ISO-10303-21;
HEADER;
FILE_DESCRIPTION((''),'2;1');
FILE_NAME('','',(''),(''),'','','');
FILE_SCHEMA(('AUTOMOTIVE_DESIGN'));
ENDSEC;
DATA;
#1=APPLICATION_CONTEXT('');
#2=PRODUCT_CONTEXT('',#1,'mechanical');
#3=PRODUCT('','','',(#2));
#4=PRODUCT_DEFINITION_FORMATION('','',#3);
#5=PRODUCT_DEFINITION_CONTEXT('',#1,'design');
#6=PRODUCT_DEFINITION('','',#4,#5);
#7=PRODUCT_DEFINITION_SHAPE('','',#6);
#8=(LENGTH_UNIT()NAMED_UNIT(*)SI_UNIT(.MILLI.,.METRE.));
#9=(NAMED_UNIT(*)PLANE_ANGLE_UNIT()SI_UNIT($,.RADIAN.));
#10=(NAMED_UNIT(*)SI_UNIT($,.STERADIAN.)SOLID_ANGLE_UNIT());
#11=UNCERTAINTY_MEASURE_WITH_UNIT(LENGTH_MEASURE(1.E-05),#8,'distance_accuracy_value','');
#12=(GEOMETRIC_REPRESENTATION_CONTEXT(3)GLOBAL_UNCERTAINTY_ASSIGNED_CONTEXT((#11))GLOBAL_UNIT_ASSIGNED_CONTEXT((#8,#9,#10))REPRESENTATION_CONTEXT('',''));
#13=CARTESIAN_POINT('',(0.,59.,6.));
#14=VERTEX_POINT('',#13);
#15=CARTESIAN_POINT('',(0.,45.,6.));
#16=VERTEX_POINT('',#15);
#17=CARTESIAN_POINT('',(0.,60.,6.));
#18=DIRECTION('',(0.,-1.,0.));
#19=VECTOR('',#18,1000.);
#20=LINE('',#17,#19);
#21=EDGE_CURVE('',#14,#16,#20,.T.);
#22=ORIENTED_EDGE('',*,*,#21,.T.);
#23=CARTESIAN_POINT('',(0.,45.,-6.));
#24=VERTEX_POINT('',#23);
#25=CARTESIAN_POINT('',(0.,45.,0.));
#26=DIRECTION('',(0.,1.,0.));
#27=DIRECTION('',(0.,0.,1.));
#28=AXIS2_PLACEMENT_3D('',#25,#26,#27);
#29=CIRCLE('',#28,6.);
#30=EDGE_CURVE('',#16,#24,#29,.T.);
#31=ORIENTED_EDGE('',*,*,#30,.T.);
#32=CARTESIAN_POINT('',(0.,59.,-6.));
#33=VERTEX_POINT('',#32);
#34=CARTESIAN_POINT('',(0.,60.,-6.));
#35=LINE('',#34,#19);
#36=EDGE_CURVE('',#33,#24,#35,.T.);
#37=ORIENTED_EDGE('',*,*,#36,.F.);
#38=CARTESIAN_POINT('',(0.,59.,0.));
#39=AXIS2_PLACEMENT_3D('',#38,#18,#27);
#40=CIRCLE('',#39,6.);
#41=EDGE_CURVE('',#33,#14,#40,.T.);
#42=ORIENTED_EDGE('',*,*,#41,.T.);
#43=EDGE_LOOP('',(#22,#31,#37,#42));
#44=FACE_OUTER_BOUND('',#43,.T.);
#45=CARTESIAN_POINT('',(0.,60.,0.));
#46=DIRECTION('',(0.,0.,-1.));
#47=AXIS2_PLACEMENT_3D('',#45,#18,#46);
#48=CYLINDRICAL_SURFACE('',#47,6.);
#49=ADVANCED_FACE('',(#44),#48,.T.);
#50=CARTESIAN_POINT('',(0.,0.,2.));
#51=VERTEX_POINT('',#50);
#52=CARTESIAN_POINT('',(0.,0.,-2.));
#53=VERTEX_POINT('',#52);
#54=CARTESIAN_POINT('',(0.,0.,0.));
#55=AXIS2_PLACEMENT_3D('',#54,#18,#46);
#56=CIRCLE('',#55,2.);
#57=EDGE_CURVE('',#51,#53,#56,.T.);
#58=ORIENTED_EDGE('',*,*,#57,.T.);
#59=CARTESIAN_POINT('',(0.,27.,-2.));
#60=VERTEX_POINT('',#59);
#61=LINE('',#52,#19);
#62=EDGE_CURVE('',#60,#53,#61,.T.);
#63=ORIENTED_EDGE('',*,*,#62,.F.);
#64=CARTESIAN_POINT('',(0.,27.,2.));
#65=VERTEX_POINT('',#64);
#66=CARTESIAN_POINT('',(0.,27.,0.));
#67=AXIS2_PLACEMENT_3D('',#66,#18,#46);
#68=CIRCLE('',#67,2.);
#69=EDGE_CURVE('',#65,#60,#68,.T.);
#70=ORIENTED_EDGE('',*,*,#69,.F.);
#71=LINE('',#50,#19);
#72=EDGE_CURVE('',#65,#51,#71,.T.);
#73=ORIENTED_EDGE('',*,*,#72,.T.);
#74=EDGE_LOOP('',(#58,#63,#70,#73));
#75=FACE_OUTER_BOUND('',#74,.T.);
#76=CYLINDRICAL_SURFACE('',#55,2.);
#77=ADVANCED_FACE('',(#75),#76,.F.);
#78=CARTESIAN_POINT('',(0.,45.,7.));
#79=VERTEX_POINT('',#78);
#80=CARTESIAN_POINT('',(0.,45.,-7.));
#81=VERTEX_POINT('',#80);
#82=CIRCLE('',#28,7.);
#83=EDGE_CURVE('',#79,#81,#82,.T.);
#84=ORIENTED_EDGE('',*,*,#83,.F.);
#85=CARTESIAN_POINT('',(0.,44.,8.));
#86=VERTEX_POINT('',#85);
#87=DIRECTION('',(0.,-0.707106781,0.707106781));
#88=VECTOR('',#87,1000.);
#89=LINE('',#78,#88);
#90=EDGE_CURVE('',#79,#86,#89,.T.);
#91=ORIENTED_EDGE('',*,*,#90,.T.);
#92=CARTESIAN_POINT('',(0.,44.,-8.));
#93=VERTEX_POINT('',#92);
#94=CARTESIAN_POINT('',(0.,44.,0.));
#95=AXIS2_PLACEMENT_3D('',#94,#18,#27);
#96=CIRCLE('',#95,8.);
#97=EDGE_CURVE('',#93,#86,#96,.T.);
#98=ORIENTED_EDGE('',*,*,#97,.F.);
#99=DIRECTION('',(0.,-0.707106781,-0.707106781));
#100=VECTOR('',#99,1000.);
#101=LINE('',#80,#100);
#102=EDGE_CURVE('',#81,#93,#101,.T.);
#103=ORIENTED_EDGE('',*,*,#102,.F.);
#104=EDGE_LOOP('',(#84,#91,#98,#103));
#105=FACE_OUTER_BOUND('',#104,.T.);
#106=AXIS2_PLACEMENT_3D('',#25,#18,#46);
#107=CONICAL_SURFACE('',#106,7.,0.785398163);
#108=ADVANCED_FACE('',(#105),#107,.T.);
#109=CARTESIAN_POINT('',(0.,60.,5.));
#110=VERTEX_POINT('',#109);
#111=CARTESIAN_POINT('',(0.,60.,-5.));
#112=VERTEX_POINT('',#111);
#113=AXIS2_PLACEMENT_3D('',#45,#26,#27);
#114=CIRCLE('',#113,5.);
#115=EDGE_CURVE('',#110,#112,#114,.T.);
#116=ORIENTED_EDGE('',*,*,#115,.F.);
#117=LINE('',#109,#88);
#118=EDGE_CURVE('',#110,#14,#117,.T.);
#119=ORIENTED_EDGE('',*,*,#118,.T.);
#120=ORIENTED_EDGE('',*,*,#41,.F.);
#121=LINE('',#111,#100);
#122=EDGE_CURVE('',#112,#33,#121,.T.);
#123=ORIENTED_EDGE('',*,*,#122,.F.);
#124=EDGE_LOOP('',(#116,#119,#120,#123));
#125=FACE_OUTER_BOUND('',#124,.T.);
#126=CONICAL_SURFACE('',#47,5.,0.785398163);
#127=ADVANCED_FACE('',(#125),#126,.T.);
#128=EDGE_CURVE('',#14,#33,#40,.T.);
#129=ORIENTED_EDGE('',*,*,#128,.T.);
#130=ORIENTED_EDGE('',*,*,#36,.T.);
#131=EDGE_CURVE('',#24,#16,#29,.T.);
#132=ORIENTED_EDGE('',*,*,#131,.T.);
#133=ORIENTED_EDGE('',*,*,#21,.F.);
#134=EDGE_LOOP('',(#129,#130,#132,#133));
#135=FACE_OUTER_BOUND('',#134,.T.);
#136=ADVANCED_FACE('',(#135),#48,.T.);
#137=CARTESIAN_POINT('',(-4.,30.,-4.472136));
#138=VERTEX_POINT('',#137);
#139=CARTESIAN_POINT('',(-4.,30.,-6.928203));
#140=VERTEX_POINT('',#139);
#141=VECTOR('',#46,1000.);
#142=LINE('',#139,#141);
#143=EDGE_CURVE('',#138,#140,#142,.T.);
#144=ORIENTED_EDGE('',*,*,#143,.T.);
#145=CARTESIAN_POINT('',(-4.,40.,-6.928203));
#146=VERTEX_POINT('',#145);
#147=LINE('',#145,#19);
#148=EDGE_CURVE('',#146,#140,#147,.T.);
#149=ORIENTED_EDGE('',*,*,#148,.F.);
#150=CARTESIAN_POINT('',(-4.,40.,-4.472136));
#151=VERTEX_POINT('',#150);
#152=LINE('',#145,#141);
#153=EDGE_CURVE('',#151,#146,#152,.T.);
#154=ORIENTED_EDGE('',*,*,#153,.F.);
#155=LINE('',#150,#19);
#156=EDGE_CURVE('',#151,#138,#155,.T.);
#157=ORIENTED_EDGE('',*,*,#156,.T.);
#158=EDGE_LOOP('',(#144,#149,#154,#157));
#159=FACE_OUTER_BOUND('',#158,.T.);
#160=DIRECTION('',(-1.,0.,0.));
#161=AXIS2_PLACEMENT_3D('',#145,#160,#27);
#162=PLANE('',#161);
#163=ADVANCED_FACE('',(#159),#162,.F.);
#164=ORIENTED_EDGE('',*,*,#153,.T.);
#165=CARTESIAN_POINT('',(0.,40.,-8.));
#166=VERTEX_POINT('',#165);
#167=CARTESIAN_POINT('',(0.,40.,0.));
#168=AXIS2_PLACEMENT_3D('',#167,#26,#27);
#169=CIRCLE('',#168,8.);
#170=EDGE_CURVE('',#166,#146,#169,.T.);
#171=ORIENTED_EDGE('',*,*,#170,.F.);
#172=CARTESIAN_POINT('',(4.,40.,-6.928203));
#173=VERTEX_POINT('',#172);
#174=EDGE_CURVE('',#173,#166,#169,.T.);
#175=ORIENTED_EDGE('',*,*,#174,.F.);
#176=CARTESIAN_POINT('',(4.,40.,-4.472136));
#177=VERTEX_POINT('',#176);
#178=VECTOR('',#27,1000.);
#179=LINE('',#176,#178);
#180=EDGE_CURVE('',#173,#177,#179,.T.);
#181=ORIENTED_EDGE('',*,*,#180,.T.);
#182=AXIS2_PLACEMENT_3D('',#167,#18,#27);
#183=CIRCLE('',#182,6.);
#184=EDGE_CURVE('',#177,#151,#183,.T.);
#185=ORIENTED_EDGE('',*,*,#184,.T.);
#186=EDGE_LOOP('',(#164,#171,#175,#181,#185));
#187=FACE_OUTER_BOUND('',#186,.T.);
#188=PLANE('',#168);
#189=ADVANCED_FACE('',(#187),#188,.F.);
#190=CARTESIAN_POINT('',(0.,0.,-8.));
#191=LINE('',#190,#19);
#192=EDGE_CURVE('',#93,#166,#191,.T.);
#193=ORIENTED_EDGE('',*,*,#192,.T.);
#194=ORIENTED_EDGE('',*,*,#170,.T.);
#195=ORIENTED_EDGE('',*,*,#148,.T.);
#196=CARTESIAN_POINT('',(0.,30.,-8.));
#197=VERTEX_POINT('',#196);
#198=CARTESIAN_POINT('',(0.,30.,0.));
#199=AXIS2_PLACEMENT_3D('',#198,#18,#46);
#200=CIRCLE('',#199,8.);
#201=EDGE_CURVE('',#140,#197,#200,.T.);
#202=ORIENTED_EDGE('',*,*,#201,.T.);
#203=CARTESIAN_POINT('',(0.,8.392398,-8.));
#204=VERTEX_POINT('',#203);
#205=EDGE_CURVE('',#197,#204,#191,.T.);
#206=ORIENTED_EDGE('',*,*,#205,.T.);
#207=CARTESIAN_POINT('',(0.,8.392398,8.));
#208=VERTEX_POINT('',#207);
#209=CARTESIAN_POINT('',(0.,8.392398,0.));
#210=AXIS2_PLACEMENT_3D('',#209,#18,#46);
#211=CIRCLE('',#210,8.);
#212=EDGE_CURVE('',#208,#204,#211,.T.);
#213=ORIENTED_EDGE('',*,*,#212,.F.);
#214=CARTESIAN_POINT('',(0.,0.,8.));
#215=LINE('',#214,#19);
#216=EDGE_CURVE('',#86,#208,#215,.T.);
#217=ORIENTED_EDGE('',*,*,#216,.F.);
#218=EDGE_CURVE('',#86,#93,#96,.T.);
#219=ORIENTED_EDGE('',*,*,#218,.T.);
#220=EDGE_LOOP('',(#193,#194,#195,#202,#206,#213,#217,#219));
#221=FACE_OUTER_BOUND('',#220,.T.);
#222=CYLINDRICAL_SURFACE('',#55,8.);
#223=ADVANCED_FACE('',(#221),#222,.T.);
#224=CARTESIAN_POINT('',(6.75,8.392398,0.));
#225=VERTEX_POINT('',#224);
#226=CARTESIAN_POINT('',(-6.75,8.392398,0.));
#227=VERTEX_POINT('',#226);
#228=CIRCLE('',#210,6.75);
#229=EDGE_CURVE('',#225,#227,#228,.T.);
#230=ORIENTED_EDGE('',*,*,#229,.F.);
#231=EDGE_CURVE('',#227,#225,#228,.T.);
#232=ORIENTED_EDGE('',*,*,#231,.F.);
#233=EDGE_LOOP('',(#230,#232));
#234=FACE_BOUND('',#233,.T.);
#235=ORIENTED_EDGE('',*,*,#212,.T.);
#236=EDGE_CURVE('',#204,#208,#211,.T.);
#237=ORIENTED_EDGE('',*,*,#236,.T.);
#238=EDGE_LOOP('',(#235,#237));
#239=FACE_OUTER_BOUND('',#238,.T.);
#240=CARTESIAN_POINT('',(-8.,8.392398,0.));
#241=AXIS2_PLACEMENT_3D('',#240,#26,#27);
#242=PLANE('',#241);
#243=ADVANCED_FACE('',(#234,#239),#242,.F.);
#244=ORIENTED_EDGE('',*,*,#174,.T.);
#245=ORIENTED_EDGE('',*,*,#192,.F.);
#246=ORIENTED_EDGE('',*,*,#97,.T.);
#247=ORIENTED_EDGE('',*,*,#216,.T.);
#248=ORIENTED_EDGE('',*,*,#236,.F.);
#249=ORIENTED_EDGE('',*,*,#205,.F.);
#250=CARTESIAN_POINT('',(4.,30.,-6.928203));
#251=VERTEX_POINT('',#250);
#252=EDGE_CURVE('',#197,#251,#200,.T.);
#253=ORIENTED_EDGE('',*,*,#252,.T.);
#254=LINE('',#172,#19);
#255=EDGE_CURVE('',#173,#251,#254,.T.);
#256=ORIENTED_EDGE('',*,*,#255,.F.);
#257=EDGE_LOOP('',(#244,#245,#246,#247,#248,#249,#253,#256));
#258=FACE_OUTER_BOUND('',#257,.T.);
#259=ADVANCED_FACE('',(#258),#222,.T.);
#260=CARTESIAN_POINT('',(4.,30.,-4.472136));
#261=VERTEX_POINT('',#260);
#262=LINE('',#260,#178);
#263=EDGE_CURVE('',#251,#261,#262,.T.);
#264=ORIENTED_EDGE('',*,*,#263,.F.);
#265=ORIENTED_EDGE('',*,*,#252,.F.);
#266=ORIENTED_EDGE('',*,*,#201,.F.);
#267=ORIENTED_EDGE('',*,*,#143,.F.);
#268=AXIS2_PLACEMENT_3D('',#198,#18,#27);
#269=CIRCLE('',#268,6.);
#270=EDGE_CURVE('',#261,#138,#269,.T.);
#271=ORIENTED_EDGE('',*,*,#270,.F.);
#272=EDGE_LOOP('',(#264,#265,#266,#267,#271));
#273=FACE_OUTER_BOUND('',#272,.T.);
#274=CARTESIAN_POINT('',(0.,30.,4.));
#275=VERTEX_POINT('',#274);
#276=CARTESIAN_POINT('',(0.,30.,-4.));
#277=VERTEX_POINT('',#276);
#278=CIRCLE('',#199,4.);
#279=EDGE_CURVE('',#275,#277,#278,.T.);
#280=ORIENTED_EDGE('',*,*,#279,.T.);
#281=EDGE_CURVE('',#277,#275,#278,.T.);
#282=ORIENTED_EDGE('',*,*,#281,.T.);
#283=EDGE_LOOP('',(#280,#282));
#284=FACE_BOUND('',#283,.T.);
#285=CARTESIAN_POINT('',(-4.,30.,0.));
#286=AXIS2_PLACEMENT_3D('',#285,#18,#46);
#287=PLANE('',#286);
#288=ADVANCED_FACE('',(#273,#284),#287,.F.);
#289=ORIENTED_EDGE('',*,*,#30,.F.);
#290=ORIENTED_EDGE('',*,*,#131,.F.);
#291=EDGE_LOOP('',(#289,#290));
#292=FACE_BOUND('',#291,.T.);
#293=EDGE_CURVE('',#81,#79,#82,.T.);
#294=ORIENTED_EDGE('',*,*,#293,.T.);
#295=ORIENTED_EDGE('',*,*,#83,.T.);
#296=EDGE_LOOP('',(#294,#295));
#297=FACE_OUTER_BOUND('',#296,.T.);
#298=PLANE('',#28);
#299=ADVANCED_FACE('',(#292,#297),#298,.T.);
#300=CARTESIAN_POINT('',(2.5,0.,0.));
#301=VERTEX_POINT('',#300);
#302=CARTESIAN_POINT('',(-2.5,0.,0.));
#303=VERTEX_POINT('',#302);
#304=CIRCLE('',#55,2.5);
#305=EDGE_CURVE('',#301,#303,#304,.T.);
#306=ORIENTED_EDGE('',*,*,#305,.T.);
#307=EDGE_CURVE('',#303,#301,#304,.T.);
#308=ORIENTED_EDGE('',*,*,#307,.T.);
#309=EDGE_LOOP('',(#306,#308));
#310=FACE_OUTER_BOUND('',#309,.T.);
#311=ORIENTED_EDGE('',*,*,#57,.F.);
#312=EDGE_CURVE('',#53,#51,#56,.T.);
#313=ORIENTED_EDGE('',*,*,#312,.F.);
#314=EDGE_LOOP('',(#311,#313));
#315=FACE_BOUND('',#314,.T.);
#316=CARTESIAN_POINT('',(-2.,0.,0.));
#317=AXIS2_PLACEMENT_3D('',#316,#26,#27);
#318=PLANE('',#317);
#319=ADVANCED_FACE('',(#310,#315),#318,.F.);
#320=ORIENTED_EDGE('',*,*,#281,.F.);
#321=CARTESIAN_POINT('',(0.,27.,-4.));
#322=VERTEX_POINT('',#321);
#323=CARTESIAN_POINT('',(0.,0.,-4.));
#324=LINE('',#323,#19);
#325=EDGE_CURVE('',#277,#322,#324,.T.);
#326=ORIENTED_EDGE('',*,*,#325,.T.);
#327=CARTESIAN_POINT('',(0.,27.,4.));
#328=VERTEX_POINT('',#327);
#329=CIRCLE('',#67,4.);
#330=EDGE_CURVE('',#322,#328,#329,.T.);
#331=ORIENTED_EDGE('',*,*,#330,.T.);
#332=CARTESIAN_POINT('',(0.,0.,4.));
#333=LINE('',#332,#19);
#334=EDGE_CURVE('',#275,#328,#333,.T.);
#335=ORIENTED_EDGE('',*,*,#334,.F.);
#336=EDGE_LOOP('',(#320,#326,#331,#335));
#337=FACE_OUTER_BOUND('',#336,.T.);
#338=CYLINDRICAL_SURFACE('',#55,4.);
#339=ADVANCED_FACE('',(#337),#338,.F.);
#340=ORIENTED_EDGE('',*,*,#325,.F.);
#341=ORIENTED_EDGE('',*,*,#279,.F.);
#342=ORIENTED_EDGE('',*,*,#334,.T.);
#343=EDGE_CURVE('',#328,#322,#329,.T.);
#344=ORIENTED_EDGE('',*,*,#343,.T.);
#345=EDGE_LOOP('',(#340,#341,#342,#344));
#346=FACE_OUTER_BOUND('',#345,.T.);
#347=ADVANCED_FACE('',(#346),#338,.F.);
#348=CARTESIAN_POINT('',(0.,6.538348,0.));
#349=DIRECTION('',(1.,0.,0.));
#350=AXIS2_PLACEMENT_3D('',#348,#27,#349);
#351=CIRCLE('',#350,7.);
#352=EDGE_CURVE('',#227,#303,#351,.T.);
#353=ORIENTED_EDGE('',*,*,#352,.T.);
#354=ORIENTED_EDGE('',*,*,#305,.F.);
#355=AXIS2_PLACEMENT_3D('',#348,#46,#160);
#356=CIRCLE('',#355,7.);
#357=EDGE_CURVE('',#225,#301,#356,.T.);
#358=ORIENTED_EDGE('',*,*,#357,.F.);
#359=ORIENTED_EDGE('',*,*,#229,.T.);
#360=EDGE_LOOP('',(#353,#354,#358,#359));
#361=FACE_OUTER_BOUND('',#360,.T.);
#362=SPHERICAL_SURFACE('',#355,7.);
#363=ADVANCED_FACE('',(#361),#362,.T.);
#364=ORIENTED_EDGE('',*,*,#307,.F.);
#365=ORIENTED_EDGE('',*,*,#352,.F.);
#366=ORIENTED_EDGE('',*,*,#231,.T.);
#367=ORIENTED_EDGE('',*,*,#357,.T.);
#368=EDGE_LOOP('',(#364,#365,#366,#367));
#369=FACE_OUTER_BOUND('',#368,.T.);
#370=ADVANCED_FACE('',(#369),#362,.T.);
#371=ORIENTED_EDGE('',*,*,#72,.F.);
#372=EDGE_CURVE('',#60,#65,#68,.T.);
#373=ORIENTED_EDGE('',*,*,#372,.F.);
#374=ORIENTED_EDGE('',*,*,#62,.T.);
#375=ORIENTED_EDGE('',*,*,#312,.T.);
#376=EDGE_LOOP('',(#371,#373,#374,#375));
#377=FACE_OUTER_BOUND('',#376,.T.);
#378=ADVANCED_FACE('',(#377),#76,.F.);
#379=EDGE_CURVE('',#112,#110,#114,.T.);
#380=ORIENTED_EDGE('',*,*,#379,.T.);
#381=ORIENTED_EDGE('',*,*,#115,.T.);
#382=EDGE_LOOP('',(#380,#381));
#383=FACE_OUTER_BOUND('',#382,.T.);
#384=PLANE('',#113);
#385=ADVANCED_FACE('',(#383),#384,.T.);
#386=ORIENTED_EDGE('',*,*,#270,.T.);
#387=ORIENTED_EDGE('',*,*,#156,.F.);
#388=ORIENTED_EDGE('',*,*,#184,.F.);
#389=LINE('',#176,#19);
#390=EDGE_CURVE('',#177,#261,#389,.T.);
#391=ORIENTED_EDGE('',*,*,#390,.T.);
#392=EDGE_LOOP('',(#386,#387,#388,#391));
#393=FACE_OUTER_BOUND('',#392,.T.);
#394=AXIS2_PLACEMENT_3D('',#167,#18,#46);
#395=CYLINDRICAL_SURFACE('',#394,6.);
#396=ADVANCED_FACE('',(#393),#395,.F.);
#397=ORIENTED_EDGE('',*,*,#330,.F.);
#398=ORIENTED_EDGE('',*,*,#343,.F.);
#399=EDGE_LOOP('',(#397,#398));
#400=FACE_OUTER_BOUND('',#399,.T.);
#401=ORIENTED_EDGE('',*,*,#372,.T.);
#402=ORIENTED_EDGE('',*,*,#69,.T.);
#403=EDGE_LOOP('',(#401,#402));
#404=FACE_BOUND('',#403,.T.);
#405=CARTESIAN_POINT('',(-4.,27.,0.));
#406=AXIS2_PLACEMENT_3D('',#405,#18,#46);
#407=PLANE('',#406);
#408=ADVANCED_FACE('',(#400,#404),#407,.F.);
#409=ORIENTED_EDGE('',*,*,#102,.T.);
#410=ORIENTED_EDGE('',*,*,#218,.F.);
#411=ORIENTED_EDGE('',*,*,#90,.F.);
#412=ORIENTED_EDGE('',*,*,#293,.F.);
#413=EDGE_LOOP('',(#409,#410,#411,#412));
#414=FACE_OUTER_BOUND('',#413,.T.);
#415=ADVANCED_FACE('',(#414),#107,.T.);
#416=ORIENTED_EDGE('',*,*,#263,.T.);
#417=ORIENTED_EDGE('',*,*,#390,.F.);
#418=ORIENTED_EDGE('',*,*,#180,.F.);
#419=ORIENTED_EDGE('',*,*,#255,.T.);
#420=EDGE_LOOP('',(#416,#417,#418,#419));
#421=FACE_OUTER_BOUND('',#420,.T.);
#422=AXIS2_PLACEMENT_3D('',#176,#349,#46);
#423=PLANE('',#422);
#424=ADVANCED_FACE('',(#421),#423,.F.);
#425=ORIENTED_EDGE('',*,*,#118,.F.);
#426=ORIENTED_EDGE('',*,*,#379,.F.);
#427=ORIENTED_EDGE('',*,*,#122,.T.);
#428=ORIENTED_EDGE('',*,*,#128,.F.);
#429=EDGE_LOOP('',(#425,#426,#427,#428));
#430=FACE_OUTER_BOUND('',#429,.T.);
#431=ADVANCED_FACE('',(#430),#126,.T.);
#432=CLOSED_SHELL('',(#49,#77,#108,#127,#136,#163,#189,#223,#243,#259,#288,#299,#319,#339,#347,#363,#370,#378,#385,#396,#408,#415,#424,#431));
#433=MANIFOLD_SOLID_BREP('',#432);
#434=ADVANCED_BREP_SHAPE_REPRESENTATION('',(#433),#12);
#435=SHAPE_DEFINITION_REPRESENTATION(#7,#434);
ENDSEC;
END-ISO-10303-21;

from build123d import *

# Parameters (mm, degrees)
BOSS_EXTRUDE1_DEPTH = 10
SKETCH3_R           = 8
BOSS_EXTRUDE2_DEPTH = 5
SKETCH4_R           = 6
BOSS_EXTRUDE3_DEPTH = 15
CHAMFER1_SIZE       = 1


with BuildPart() as part:
    # Sketch1 → Revolve2 (revolve)
    with BuildSketch(Plane.XY, mode=Mode.PRIVATE) as revolve2_sk:
        with BuildLine():
            Line((-2, 0), (-2, 27))
            Line((-2, 27), (-4, 27))
            Line((-4, 27), (-4, 30))
            Line((-4, 30), (-8, 30))
            Line((-8, 30), (-8, 8.392398037))
            Line((-8, 8.392398037), (-6.75, 8.392398037))
            ThreePointArc((-6.75, 8.392398037), (-6.244894811, 3.375866985), (-2.5, 0))
            Line((-2.5, 0), (-2, 0))
        make_face()
    revolve(revolve2_sk.sketch.rotate(Axis((0, 0, 0), (0, 1, 0)), 270), axis=Axis((0, 0, 0), (0, 1, 0)))

    # Sketch2 → Boss-Extrude1 (add)
    with BuildSketch(Plane(origin=(0, 30, 0), x_dir=(1, 0, 0), z_dir=(0, 1, 0))):
        with BuildLine():
            Line((-4, 6.92820323), (-4, 4.472135955))
            ThreePointArc((-4, 4.472135955), (0, -6), (4, 4.472135955))
            Line((4, 4.472135955), (4, 6.92820323))
            ThreePointArc((4, 6.92820323), (0, -8), (-4, 6.92820323))
        make_face()
    extrude(amount=BOSS_EXTRUDE1_DEPTH)

    # Sketch3 → Boss-Extrude2 (add)
    with BuildSketch(Plane(origin=(0, 40, 0), x_dir=(1, 0, 0), z_dir=(0, 1, 0))):
        with Locations(Location((0, 0, 0), (0, 0, 90))):
            Circle(SKETCH3_R)
    extrude(amount=BOSS_EXTRUDE2_DEPTH)

    # Sketch4 → Boss-Extrude3 (add)
    with BuildSketch(Plane(origin=(0, 45, 0), x_dir=(1, 0, 0), z_dir=(0, 1, 0))):
        with Locations(Location((0, 0, 0), (0, 0, 270))):
            Circle(SKETCH4_R)
    extrude(amount=BOSS_EXTRUDE3_DEPTH)

    # Chamfer1
    chamfer1_edges = [part.edges().sort_by_distance(p)[0] for p in [
        (0, 45, 8),
        (0, 60, -6),
    ]]
    chamfer(chamfer1_edges, length=CHAMFER1_SIZE)


solid = part.part
